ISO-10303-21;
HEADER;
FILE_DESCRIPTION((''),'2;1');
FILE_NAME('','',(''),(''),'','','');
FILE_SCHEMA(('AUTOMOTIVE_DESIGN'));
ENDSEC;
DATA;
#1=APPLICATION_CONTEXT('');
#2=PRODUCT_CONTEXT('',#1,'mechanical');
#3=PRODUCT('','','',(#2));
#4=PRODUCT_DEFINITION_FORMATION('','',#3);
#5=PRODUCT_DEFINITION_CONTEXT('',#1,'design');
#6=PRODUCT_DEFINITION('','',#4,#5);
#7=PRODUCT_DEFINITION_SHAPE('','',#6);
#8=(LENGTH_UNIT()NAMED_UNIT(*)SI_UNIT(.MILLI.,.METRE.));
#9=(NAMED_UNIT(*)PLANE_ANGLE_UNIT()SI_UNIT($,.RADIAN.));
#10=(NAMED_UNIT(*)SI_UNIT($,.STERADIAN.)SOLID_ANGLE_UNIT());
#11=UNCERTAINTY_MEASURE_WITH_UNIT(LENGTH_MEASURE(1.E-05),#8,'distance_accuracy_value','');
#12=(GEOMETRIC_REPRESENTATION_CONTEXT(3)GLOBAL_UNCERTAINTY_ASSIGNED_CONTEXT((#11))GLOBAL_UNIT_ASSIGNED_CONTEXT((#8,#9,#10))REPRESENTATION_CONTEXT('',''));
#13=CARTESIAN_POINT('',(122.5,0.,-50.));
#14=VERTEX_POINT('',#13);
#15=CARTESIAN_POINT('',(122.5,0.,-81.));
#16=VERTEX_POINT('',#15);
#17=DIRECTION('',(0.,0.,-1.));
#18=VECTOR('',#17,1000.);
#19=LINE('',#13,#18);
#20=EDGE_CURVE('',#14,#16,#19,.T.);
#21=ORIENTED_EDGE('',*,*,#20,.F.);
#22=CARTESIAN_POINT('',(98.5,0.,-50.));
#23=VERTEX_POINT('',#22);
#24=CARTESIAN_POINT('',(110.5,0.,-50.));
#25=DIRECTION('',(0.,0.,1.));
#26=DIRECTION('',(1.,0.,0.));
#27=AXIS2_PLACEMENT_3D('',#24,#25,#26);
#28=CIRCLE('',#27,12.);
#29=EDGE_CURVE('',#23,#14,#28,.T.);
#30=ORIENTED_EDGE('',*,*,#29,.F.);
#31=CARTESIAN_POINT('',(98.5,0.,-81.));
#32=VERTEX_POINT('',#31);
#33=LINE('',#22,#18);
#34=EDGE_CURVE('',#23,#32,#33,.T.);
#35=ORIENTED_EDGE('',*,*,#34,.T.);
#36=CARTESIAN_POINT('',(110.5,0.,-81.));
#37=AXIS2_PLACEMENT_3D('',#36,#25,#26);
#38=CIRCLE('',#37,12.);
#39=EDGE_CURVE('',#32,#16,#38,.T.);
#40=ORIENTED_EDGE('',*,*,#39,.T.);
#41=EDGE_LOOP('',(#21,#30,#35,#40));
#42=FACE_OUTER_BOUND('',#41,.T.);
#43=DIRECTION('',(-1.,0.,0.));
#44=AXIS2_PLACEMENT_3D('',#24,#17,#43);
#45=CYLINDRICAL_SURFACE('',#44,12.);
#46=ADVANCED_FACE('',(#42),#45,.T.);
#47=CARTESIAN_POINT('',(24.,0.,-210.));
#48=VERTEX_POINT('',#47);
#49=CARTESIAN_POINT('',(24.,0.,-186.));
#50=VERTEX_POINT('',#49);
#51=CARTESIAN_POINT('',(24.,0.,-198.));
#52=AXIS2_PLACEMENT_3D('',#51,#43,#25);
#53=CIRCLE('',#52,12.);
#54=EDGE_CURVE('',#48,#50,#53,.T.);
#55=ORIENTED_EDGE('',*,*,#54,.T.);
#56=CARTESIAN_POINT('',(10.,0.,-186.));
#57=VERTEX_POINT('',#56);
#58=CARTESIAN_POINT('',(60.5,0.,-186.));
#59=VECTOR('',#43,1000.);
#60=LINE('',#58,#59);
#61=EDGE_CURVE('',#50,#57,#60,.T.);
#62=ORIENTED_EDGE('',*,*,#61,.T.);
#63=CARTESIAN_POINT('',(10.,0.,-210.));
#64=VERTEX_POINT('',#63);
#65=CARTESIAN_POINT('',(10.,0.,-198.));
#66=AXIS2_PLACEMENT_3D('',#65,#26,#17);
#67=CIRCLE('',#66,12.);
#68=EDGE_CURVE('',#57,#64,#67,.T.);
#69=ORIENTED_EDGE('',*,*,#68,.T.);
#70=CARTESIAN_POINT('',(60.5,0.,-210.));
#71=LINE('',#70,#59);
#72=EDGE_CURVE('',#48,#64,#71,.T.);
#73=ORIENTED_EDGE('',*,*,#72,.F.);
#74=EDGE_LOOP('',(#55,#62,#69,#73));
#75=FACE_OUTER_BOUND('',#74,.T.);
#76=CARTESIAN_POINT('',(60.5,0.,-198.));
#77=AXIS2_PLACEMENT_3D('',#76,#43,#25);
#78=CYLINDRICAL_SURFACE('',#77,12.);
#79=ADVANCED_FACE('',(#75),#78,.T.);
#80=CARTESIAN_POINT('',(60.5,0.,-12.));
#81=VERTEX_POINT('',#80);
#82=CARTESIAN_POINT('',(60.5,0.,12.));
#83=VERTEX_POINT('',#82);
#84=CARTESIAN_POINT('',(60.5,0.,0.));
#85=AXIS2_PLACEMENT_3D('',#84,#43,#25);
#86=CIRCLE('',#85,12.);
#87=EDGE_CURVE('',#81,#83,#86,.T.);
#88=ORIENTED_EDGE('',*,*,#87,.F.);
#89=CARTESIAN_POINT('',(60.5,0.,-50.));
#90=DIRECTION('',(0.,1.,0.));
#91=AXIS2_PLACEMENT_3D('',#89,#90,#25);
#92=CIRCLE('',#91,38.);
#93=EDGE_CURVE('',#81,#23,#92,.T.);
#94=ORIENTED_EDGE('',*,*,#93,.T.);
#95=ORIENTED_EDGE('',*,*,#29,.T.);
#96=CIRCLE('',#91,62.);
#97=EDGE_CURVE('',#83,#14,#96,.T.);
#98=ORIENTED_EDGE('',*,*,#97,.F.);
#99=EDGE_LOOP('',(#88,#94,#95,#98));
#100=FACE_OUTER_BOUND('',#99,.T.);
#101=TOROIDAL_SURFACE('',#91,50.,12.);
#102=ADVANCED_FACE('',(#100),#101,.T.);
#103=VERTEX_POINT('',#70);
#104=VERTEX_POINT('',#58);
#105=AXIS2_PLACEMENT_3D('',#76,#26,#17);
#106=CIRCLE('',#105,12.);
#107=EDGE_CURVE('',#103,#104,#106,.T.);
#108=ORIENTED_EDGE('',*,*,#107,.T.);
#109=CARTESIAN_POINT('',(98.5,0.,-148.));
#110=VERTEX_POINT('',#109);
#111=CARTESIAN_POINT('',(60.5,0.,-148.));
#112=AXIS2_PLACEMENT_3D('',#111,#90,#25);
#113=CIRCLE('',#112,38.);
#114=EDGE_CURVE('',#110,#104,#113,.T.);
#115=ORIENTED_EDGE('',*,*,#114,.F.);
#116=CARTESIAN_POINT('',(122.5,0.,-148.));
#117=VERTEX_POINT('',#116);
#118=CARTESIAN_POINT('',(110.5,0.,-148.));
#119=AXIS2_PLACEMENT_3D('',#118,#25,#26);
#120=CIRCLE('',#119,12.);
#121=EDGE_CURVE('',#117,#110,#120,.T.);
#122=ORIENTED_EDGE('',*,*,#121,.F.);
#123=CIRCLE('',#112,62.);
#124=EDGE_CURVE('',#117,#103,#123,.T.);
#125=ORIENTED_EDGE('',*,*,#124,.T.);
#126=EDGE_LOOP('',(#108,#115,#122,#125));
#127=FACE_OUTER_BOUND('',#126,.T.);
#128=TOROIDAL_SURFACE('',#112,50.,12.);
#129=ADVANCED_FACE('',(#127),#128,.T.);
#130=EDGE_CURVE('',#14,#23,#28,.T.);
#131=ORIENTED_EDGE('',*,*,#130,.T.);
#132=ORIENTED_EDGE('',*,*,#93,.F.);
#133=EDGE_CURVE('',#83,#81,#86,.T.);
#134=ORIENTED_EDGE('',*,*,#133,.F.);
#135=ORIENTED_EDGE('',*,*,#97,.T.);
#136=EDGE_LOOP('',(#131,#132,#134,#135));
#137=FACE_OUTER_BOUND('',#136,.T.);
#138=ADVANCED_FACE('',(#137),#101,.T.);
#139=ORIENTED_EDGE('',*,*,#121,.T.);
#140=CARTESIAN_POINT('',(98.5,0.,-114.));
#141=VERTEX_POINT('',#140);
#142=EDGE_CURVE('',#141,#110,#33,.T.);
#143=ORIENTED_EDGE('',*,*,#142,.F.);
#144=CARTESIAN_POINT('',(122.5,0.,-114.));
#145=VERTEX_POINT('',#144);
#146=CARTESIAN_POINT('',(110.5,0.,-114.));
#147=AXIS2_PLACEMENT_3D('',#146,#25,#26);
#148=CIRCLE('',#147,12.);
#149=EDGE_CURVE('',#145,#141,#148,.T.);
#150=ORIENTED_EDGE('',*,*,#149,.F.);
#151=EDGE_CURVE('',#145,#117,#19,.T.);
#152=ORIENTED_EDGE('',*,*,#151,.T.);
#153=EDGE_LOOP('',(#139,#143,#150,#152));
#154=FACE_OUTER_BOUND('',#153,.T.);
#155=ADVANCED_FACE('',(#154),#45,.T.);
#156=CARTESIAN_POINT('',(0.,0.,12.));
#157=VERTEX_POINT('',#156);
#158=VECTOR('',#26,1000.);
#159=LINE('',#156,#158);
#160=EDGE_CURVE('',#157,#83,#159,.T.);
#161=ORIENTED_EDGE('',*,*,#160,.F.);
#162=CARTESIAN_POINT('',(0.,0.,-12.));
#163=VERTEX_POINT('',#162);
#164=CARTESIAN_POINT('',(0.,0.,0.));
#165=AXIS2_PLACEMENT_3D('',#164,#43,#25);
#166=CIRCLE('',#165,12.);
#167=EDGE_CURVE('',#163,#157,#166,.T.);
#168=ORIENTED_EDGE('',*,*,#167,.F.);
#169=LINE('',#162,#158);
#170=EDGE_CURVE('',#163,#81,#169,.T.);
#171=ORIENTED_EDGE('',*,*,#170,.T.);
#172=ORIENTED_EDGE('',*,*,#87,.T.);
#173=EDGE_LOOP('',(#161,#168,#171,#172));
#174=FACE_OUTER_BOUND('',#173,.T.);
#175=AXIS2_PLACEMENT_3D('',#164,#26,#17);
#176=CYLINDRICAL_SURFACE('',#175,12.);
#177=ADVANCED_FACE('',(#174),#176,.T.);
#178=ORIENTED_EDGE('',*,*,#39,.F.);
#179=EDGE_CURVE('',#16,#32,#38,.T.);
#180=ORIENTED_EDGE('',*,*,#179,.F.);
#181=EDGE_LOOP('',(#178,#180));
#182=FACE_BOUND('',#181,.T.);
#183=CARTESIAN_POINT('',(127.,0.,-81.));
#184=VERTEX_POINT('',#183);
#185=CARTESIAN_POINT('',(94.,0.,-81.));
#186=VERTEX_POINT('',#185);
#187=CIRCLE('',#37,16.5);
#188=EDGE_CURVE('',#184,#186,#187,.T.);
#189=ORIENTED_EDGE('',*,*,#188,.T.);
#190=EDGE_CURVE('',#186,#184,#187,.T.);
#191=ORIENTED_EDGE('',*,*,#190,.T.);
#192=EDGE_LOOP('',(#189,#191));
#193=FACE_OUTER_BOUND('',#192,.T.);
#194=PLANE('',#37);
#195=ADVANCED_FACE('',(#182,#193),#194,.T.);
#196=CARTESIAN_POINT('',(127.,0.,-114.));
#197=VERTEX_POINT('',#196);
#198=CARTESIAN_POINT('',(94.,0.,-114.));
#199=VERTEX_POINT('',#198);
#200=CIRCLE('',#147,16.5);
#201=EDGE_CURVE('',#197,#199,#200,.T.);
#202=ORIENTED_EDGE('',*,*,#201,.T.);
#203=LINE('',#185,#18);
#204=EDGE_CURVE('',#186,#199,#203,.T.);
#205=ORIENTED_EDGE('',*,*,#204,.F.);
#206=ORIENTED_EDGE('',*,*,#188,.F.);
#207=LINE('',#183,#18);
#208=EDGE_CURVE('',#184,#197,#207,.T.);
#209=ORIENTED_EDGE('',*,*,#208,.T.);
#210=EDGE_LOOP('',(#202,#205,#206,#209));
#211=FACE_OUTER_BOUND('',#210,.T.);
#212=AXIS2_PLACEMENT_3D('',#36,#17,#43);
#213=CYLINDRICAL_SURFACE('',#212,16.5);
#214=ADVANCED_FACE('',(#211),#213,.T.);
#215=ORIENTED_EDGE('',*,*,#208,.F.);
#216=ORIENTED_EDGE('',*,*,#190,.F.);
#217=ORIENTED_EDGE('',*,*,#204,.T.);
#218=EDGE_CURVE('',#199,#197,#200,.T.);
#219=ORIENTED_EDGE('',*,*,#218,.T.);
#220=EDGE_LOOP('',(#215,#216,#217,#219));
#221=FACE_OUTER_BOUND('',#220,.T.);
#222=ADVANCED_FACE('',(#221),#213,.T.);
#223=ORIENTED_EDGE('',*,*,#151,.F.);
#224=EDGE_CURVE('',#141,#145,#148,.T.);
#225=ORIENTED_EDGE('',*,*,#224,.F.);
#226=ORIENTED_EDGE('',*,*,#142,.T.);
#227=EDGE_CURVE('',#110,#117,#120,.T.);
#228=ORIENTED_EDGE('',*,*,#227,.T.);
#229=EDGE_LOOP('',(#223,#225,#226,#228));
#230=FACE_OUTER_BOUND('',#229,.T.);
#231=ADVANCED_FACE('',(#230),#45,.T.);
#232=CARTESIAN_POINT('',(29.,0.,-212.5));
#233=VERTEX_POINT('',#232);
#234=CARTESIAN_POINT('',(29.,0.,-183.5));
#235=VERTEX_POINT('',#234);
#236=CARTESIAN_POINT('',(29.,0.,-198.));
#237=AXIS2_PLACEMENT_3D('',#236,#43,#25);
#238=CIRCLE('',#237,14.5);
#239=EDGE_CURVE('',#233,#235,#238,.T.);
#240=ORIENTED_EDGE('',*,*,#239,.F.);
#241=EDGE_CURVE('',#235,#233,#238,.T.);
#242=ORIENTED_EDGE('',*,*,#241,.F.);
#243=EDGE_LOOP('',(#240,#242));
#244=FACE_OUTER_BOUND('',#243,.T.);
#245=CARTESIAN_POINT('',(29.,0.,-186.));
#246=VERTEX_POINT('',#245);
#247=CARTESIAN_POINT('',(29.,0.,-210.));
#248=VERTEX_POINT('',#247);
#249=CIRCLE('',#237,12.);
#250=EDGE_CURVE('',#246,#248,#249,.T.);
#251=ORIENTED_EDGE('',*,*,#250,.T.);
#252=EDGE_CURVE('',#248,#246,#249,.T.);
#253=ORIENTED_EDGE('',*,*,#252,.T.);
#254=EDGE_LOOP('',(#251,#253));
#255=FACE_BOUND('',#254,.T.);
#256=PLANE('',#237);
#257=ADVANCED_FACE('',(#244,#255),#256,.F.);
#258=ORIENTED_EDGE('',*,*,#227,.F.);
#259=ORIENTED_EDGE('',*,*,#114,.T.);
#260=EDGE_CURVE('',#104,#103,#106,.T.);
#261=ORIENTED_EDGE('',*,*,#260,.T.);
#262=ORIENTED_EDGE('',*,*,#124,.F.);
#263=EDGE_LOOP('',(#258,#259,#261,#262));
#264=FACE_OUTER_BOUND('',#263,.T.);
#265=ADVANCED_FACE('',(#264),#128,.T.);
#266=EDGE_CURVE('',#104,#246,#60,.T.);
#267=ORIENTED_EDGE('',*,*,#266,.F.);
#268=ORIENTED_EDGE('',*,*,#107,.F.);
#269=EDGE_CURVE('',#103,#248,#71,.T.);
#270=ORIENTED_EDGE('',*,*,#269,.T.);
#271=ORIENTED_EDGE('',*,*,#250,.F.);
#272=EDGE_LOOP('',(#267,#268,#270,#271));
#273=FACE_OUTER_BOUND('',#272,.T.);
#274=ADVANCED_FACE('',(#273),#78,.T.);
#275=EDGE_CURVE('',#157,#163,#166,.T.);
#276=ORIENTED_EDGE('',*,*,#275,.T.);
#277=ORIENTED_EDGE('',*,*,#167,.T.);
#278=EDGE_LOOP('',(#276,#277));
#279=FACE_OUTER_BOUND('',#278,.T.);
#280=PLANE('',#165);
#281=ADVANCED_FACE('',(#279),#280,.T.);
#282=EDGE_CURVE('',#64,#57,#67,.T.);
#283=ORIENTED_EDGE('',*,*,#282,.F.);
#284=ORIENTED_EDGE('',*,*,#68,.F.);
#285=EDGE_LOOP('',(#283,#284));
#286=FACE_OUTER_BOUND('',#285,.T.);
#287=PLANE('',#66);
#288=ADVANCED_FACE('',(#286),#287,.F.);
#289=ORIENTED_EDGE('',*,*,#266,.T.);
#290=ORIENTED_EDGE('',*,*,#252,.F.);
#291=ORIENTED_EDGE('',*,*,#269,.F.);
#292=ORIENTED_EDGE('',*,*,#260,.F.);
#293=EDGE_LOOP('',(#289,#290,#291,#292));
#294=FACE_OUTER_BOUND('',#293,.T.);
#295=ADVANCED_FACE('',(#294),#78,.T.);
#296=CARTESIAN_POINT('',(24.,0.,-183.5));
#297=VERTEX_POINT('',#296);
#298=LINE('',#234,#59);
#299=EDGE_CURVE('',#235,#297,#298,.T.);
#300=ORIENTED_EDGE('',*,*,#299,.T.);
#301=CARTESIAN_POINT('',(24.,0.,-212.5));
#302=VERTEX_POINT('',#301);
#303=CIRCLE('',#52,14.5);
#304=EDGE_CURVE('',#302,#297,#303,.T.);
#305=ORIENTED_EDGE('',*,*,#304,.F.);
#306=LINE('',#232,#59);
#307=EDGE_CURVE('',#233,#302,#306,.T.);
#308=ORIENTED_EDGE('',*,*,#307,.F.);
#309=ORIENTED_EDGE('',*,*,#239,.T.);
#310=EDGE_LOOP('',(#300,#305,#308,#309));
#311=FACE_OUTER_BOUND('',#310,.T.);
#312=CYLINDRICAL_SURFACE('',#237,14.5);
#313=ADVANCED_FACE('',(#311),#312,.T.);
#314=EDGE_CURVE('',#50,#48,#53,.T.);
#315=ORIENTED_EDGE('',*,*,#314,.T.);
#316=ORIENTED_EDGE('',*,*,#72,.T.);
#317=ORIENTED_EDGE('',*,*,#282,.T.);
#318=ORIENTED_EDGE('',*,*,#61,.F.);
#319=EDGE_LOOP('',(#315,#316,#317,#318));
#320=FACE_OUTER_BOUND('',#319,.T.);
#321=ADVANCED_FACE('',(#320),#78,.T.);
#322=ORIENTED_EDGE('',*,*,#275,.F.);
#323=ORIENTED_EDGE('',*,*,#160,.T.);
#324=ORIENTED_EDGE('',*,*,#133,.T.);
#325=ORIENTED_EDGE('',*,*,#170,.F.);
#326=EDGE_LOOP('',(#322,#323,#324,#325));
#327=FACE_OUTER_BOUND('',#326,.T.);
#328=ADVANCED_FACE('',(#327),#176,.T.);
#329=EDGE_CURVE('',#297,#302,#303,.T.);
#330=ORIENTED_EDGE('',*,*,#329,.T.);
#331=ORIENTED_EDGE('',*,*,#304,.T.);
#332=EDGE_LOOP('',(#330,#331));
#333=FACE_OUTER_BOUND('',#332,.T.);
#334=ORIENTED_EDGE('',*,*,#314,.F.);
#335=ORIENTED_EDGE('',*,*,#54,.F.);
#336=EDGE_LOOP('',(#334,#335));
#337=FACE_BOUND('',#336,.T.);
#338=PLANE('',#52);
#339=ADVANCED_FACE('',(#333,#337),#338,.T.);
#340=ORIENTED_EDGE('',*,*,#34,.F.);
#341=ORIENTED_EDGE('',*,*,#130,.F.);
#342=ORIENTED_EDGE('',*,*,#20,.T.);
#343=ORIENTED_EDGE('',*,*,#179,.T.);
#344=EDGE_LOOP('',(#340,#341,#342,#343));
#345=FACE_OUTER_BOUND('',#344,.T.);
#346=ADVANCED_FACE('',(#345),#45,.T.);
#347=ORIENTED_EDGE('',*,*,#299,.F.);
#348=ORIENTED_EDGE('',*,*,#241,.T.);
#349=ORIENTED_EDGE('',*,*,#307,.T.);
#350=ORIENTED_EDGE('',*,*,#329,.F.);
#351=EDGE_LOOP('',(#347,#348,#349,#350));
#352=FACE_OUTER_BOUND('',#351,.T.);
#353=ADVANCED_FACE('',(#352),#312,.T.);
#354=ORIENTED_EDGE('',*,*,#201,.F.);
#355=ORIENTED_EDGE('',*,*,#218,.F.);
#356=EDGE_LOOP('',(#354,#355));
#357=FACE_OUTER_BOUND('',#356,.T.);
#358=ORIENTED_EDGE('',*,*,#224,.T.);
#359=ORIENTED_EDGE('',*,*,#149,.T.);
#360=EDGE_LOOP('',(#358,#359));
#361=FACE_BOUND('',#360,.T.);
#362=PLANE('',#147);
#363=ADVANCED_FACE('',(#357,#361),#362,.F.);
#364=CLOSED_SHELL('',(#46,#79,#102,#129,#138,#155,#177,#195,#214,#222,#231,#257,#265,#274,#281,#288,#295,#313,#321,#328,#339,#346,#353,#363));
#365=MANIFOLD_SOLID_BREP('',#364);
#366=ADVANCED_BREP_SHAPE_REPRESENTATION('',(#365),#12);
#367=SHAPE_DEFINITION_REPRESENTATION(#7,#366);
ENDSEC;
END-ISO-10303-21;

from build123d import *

# Parameters (mm, degrees)
SWEEP_1_PROFILE_R = 12
EXTRUDE_START     = -14
SKETCH_14_R       = 14.5
EXTRUDE_1_DEPTH   = 5
SKETCH_16_R       = 16.5
EXTRUDE_2_DEPTH   = 16.5


with BuildPart() as part:
    # 扫描1: sweep along a path in 草图1
    with BuildLine(Plane(origin=(0, 0, 0), x_dir=(1, 0, 0), z_dir=(0, 1, 0))) as sweep_1_path:
        Line((0, 0), (60.5, 0))
        ThreePointArc((60.5, 0), (95.855339059, 14.644660941), (110.5, 50))
        Line((110.5, 50), (110.5, 148))
        ThreePointArc((110.5, 148), (95.855339059, 183.355339059), (60.5, 198))
        Line((60.5, 198), (10, 198))
    # 扫描1 profile (on start of the path) → 扫描1 (sweep)
    with BuildSketch(Plane(origin=(0, 0, 0), x_dir=(0, 0, 1), z_dir=(1, 0, 0))):
        Circle(SWEEP_1_PROFILE_R)
    sweep(path=sweep_1_path.line)

    # 草图14 → 凸台-拉伸1 (add)
    with BuildSketch(Plane.ZY.offset(-10).offset(EXTRUDE_START)):
        with Locations((-198, 0)):
            Circle(SKETCH_14_R)
    extrude(amount=-EXTRUDE_1_DEPTH)

    # 草图16 → 凸台-拉伸2 (add, symmetric)
    with BuildSketch(Plane.XY.offset(-97.5)):
        with Locations((110.5, 0)):
            Circle(SKETCH_16_R)
    extrude(amount=EXTRUDE_2_DEPTH, both=True)


solid = part.part
